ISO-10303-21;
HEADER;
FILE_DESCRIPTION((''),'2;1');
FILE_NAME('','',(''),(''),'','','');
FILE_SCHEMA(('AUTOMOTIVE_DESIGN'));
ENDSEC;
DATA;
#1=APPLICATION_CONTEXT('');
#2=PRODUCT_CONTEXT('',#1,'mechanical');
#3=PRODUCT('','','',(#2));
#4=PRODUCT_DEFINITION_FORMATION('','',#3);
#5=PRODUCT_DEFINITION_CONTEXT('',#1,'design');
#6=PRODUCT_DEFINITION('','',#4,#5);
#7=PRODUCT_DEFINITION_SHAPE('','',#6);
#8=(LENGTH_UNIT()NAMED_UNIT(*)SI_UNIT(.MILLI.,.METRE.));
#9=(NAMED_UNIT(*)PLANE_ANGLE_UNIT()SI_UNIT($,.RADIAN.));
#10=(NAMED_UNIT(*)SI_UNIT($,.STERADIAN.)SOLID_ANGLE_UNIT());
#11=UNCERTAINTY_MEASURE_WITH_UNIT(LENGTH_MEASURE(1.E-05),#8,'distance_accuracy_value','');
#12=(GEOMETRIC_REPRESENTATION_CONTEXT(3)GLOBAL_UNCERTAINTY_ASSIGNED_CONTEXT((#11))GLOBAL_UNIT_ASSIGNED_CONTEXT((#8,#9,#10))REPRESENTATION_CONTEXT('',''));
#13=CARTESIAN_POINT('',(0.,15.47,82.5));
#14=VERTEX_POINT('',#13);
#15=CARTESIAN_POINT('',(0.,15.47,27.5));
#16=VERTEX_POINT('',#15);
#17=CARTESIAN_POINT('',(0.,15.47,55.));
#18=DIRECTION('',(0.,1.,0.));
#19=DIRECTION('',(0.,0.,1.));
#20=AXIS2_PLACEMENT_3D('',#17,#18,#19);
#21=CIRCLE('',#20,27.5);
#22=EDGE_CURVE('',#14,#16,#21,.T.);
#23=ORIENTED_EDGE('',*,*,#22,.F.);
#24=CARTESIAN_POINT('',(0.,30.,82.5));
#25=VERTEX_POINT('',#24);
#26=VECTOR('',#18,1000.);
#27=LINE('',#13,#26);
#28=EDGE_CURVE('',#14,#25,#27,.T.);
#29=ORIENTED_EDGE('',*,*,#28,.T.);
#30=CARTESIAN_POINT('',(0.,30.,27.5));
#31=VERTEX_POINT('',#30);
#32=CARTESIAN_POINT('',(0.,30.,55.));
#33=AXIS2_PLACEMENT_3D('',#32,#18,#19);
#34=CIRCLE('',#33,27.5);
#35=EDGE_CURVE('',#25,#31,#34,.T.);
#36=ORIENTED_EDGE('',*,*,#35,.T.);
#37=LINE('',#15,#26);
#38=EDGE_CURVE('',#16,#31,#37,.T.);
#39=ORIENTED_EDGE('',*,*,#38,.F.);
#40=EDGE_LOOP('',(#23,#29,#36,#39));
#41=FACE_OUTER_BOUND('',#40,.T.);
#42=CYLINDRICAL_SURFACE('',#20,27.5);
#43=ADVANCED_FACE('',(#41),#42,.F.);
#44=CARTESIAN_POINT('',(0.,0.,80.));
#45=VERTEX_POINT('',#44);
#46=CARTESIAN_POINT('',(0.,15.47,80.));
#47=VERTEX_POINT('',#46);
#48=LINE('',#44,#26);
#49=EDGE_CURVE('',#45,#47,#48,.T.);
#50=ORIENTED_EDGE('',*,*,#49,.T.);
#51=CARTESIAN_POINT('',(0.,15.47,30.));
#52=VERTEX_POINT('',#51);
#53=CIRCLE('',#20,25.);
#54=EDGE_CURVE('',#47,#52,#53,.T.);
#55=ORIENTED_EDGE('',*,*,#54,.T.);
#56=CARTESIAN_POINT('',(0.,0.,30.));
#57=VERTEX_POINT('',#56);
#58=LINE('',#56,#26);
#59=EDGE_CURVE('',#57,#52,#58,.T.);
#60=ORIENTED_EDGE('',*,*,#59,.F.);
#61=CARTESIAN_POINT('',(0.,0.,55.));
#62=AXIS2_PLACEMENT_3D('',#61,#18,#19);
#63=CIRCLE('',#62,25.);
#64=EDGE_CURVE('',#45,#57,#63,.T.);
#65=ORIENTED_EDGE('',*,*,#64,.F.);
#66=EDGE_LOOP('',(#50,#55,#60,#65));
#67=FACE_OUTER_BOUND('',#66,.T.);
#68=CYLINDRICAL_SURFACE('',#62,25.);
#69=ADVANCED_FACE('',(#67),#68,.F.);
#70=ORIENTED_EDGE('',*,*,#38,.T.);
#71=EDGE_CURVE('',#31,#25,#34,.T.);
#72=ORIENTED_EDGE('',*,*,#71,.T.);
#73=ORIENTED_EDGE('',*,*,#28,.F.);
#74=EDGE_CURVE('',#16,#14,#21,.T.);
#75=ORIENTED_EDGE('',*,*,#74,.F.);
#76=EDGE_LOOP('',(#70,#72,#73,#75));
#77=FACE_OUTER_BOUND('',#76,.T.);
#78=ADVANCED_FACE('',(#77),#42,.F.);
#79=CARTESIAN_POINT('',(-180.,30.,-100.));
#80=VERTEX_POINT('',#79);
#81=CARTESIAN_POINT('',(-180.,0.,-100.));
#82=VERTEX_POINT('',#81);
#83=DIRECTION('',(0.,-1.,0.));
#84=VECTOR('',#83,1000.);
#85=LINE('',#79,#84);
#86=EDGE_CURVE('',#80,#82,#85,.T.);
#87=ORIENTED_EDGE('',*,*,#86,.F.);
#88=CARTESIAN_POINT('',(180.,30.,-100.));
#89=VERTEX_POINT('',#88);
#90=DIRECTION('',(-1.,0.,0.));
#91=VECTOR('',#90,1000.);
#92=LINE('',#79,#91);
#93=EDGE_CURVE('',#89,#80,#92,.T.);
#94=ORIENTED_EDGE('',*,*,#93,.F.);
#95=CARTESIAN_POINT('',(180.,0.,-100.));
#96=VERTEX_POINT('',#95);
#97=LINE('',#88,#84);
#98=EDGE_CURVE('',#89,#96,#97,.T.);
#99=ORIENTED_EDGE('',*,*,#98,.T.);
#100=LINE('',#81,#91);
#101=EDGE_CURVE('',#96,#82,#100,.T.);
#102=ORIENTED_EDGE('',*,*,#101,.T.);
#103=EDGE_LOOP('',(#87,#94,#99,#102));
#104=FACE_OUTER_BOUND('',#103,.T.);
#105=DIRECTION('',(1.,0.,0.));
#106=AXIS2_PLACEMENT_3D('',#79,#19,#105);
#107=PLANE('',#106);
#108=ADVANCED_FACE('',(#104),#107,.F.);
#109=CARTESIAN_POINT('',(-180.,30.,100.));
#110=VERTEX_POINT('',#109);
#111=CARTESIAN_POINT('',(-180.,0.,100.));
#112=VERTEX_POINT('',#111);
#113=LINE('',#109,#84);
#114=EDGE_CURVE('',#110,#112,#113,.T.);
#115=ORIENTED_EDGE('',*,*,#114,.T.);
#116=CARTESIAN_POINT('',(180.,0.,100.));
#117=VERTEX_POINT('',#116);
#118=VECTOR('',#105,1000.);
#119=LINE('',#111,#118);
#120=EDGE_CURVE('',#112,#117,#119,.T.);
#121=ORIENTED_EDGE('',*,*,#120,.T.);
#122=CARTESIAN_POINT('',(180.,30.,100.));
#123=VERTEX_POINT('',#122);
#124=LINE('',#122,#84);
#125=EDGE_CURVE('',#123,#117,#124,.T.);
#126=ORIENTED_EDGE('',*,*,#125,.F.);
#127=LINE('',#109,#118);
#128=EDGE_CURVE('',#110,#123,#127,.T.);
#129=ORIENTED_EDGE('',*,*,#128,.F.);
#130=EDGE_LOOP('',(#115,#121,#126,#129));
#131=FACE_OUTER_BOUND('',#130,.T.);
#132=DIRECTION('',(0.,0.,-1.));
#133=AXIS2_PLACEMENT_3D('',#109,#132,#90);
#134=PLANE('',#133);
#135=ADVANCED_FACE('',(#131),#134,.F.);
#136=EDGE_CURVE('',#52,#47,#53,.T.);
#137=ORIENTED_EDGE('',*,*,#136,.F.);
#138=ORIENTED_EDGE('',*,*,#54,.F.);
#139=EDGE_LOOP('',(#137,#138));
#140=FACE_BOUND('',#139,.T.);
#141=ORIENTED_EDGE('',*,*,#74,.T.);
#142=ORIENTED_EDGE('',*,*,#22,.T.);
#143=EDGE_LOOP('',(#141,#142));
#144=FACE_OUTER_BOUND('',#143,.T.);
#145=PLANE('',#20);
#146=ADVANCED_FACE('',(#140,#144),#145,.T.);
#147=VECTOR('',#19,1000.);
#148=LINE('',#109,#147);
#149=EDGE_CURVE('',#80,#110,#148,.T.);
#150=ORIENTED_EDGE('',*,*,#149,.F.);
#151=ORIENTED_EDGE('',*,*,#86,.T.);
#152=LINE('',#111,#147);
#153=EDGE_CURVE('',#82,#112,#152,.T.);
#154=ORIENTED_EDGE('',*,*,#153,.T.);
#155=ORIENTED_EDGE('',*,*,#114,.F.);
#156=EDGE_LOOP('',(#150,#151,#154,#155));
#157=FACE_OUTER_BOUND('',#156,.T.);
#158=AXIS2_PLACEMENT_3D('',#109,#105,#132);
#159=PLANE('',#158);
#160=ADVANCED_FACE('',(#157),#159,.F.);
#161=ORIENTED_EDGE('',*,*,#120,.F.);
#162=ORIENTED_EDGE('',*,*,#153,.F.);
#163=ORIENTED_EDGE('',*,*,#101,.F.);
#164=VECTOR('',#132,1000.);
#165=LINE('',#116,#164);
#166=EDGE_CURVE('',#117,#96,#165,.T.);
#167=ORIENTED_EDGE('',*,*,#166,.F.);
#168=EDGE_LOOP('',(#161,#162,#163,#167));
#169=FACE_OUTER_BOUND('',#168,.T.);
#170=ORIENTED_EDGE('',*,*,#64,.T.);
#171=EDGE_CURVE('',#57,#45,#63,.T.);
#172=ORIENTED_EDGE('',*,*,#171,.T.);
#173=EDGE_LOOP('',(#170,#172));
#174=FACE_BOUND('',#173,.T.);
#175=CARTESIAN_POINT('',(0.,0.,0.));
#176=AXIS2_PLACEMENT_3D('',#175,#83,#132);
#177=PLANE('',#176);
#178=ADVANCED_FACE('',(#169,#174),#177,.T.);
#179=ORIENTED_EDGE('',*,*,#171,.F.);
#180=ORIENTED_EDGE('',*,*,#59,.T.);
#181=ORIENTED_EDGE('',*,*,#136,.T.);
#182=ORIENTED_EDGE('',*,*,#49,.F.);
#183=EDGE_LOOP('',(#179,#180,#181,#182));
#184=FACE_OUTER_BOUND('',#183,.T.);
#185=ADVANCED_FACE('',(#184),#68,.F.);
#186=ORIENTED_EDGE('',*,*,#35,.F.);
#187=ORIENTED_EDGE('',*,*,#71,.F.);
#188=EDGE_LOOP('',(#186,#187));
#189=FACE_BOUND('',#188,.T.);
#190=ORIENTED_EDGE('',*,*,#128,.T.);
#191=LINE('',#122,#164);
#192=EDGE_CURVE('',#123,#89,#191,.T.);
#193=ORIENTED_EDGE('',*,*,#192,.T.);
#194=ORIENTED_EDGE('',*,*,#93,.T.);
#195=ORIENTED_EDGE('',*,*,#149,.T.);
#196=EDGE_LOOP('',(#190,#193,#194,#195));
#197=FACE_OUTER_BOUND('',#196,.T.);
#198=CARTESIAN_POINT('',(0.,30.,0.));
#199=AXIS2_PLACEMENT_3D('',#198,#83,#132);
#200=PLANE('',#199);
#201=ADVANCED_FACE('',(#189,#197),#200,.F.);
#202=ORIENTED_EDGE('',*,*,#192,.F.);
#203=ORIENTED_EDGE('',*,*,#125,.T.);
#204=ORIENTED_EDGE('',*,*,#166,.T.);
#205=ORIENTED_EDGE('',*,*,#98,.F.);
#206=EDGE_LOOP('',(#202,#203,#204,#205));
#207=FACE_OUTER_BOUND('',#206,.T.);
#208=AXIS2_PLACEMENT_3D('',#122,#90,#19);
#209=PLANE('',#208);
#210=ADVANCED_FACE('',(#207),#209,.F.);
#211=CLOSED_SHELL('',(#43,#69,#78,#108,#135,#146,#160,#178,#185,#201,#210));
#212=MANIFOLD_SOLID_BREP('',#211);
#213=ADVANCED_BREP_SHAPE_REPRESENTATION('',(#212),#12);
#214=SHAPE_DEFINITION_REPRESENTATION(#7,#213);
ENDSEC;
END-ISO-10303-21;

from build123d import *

# Parameters (mm, degrees)
SKETCH_1_W          = 360
SKETCH_1_H          = 200
EXTRUDE_1_DEPTH     = 30
SKETCH_2_R          = 27.5
CUT_EXTRUDE_1_DEPTH = 14.53
SKETCH_3_R          = 25
CUT_EXTRUDE_2_DEPTH = 209.086520467


with BuildPart() as part:
    # 草图1 → 凸台-拉伸1 (new body)
    with BuildSketch(Plane(origin=(0, 0, 0), x_dir=(1, 0, 0), z_dir=(0, 1, 0))):
        Rectangle(SKETCH_1_W, SKETCH_1_H)
    extrude(amount=EXTRUDE_1_DEPTH)

    # 草图2 → 切除-拉伸1 (cut)
    with BuildSketch(Plane(origin=(0, 30, 0), x_dir=(1, 0, 0), z_dir=(0, 1, 0))):
        with Locations(Location((0, -55, 0), (0, 0, 270))):
            Circle(SKETCH_2_R)
    extrude(amount=-CUT_EXTRUDE_1_DEPTH, mode=Mode.SUBTRACT)

    # 草图3 → 切除-拉伸2 (cut, through all)
    with BuildSketch(Plane(origin=(0, 30, 0), x_dir=(1, 0, 0), z_dir=(0, 1, 0))):
        with Locations(Location((0, -55, 0), (0, 0, 270))):
            Circle(SKETCH_3_R)
    extrude(amount=-CUT_EXTRUDE_2_DEPTH, mode=Mode.SUBTRACT)


solid = part.part
